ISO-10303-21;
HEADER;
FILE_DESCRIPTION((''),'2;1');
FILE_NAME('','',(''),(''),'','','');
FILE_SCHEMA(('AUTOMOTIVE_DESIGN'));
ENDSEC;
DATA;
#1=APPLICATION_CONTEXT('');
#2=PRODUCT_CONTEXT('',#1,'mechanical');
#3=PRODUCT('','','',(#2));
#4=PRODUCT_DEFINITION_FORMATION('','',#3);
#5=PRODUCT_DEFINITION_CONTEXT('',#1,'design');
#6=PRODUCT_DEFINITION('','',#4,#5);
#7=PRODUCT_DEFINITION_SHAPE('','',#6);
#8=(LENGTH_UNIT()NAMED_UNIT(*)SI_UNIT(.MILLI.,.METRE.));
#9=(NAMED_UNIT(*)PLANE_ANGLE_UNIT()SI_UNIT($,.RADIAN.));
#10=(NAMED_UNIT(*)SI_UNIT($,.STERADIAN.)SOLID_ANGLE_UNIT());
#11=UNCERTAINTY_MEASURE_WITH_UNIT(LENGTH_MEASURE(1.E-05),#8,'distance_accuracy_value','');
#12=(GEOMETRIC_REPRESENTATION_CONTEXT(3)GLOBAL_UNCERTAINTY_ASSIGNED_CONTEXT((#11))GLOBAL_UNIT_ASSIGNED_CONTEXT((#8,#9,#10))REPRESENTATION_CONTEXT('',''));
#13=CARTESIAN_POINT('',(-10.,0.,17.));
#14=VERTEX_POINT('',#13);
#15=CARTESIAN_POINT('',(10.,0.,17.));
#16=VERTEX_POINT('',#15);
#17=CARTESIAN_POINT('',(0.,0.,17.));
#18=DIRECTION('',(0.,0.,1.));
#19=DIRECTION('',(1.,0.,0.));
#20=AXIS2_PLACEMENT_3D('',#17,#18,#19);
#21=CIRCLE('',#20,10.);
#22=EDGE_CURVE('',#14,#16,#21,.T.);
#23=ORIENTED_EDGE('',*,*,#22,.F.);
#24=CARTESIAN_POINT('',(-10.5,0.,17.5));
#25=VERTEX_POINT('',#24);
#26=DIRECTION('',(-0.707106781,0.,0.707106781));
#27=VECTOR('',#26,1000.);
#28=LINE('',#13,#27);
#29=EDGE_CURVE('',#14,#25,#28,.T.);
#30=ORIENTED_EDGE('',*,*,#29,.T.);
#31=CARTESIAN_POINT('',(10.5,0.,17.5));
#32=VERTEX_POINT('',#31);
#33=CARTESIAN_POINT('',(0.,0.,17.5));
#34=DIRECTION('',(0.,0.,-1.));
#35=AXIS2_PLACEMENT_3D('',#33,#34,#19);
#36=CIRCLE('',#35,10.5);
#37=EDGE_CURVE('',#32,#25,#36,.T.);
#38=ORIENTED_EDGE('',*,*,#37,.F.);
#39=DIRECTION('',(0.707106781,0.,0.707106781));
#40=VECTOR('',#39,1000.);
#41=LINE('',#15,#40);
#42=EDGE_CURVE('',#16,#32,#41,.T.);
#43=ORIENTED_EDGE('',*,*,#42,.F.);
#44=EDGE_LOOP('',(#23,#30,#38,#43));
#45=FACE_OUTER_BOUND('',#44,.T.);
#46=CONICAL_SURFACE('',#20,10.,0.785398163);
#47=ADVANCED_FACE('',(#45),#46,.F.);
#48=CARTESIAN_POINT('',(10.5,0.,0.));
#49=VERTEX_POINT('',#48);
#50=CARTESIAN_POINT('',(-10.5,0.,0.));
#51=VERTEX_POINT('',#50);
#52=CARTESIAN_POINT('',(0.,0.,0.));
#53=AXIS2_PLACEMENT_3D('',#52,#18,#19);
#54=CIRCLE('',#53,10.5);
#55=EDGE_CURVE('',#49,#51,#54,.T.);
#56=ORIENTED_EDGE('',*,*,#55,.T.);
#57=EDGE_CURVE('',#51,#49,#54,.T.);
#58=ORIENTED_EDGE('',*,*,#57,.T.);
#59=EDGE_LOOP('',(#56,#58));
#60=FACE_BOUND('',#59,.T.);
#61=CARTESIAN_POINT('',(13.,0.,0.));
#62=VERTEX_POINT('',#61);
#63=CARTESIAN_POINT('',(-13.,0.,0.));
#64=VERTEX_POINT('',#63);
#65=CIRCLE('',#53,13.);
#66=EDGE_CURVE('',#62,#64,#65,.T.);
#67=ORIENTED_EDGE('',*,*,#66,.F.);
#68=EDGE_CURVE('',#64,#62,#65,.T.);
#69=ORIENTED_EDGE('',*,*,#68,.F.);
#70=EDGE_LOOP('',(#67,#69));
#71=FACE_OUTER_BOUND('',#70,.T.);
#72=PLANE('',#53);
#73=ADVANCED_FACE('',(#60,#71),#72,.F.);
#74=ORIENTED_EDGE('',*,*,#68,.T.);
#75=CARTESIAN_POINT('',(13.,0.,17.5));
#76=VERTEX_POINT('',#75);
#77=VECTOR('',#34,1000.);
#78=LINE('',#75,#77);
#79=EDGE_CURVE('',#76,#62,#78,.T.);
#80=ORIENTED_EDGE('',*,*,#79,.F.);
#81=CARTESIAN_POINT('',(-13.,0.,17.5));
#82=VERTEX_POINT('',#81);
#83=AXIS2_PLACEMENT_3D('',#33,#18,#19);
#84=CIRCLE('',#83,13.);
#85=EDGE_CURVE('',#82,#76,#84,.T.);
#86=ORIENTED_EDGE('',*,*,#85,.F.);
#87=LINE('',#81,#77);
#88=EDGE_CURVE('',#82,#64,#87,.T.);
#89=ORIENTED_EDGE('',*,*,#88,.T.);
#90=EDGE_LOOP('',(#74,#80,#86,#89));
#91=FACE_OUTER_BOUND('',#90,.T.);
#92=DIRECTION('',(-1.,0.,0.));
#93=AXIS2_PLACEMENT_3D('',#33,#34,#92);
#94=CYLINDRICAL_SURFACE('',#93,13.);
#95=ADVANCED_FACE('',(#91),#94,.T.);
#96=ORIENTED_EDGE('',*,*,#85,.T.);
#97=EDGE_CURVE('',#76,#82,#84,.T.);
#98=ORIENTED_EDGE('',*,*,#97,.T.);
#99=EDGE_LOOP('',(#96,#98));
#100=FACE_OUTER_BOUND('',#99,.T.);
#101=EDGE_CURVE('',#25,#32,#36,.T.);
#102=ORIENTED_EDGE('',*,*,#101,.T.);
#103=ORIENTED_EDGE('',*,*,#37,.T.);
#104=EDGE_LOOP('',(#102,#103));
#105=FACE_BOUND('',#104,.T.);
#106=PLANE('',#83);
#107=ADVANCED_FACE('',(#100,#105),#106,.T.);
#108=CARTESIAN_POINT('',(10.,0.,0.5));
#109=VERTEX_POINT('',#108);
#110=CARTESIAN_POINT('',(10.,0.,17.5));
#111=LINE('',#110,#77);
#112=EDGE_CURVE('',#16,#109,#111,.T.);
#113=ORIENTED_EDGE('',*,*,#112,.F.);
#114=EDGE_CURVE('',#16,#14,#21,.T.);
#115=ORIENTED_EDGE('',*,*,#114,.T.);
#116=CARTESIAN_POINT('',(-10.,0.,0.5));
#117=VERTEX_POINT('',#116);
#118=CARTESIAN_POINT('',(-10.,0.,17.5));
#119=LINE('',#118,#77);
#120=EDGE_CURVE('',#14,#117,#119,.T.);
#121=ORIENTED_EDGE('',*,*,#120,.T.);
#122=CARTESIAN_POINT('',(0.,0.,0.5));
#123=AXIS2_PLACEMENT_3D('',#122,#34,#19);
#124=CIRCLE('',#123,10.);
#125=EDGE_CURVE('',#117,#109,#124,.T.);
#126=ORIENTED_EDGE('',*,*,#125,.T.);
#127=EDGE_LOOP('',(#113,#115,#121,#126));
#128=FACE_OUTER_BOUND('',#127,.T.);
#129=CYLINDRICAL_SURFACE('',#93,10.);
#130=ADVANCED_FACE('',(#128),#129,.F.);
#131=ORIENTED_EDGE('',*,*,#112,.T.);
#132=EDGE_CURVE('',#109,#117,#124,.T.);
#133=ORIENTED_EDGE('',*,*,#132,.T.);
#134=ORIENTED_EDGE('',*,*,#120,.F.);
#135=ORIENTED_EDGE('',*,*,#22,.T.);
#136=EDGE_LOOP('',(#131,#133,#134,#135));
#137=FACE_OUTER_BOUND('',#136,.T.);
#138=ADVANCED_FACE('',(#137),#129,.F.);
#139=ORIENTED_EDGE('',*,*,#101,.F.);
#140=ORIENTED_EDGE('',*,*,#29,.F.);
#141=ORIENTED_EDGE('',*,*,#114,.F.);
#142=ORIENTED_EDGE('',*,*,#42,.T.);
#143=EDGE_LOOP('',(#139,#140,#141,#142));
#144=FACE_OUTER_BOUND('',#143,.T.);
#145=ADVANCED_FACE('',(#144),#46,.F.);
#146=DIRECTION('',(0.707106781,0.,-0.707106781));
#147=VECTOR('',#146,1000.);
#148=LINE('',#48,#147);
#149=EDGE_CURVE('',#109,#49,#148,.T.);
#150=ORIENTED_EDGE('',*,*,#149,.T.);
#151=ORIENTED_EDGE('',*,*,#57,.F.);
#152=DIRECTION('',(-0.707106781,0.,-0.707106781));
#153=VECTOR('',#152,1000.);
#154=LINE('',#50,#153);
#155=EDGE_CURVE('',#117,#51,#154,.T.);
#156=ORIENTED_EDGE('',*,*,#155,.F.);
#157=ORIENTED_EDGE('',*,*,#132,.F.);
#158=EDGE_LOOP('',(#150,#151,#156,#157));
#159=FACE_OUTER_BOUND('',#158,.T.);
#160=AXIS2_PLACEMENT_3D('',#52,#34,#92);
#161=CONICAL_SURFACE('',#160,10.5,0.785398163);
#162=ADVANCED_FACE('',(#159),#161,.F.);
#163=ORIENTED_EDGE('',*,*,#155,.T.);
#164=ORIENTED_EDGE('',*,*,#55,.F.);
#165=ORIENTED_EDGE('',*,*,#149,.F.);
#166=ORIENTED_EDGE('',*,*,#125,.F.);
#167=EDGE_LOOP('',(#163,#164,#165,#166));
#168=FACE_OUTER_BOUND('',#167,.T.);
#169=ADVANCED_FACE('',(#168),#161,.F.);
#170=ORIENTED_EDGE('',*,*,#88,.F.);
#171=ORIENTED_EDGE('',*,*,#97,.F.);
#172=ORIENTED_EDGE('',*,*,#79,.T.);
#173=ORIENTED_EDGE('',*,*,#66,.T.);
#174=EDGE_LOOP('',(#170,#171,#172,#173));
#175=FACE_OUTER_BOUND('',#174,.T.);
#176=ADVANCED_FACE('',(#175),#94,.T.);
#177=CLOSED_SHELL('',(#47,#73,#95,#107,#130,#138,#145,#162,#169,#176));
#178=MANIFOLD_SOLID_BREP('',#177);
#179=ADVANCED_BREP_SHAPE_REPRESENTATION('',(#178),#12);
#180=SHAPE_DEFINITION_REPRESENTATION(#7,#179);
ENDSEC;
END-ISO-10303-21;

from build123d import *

# Parameters (mm, degrees)
SKETCH1_R           = 13
SKETCH1_R_2         = 10
BOSS_EXTRUDE1_DEPTH = 17.5
CHAMFER1_SIZE       = 0.5


with BuildPart() as part:
    # Sketch1 → Boss-Extrude1 (new body)
    with BuildSketch(Plane.XY):
        Circle(SKETCH1_R)
        Circle(SKETCH1_R_2, mode=Mode.SUBTRACT)
    extrude(amount=BOSS_EXTRUDE1_DEPTH)

    # Chamfer1
    chamfer1_edges = [part.edges().sort_by_distance(p)[0] for p in [
        (-10, 0, 0),
        (-10, 0, 17.5),
    ]]
    chamfer(chamfer1_edges, length=CHAMFER1_SIZE)


solid = part.part
